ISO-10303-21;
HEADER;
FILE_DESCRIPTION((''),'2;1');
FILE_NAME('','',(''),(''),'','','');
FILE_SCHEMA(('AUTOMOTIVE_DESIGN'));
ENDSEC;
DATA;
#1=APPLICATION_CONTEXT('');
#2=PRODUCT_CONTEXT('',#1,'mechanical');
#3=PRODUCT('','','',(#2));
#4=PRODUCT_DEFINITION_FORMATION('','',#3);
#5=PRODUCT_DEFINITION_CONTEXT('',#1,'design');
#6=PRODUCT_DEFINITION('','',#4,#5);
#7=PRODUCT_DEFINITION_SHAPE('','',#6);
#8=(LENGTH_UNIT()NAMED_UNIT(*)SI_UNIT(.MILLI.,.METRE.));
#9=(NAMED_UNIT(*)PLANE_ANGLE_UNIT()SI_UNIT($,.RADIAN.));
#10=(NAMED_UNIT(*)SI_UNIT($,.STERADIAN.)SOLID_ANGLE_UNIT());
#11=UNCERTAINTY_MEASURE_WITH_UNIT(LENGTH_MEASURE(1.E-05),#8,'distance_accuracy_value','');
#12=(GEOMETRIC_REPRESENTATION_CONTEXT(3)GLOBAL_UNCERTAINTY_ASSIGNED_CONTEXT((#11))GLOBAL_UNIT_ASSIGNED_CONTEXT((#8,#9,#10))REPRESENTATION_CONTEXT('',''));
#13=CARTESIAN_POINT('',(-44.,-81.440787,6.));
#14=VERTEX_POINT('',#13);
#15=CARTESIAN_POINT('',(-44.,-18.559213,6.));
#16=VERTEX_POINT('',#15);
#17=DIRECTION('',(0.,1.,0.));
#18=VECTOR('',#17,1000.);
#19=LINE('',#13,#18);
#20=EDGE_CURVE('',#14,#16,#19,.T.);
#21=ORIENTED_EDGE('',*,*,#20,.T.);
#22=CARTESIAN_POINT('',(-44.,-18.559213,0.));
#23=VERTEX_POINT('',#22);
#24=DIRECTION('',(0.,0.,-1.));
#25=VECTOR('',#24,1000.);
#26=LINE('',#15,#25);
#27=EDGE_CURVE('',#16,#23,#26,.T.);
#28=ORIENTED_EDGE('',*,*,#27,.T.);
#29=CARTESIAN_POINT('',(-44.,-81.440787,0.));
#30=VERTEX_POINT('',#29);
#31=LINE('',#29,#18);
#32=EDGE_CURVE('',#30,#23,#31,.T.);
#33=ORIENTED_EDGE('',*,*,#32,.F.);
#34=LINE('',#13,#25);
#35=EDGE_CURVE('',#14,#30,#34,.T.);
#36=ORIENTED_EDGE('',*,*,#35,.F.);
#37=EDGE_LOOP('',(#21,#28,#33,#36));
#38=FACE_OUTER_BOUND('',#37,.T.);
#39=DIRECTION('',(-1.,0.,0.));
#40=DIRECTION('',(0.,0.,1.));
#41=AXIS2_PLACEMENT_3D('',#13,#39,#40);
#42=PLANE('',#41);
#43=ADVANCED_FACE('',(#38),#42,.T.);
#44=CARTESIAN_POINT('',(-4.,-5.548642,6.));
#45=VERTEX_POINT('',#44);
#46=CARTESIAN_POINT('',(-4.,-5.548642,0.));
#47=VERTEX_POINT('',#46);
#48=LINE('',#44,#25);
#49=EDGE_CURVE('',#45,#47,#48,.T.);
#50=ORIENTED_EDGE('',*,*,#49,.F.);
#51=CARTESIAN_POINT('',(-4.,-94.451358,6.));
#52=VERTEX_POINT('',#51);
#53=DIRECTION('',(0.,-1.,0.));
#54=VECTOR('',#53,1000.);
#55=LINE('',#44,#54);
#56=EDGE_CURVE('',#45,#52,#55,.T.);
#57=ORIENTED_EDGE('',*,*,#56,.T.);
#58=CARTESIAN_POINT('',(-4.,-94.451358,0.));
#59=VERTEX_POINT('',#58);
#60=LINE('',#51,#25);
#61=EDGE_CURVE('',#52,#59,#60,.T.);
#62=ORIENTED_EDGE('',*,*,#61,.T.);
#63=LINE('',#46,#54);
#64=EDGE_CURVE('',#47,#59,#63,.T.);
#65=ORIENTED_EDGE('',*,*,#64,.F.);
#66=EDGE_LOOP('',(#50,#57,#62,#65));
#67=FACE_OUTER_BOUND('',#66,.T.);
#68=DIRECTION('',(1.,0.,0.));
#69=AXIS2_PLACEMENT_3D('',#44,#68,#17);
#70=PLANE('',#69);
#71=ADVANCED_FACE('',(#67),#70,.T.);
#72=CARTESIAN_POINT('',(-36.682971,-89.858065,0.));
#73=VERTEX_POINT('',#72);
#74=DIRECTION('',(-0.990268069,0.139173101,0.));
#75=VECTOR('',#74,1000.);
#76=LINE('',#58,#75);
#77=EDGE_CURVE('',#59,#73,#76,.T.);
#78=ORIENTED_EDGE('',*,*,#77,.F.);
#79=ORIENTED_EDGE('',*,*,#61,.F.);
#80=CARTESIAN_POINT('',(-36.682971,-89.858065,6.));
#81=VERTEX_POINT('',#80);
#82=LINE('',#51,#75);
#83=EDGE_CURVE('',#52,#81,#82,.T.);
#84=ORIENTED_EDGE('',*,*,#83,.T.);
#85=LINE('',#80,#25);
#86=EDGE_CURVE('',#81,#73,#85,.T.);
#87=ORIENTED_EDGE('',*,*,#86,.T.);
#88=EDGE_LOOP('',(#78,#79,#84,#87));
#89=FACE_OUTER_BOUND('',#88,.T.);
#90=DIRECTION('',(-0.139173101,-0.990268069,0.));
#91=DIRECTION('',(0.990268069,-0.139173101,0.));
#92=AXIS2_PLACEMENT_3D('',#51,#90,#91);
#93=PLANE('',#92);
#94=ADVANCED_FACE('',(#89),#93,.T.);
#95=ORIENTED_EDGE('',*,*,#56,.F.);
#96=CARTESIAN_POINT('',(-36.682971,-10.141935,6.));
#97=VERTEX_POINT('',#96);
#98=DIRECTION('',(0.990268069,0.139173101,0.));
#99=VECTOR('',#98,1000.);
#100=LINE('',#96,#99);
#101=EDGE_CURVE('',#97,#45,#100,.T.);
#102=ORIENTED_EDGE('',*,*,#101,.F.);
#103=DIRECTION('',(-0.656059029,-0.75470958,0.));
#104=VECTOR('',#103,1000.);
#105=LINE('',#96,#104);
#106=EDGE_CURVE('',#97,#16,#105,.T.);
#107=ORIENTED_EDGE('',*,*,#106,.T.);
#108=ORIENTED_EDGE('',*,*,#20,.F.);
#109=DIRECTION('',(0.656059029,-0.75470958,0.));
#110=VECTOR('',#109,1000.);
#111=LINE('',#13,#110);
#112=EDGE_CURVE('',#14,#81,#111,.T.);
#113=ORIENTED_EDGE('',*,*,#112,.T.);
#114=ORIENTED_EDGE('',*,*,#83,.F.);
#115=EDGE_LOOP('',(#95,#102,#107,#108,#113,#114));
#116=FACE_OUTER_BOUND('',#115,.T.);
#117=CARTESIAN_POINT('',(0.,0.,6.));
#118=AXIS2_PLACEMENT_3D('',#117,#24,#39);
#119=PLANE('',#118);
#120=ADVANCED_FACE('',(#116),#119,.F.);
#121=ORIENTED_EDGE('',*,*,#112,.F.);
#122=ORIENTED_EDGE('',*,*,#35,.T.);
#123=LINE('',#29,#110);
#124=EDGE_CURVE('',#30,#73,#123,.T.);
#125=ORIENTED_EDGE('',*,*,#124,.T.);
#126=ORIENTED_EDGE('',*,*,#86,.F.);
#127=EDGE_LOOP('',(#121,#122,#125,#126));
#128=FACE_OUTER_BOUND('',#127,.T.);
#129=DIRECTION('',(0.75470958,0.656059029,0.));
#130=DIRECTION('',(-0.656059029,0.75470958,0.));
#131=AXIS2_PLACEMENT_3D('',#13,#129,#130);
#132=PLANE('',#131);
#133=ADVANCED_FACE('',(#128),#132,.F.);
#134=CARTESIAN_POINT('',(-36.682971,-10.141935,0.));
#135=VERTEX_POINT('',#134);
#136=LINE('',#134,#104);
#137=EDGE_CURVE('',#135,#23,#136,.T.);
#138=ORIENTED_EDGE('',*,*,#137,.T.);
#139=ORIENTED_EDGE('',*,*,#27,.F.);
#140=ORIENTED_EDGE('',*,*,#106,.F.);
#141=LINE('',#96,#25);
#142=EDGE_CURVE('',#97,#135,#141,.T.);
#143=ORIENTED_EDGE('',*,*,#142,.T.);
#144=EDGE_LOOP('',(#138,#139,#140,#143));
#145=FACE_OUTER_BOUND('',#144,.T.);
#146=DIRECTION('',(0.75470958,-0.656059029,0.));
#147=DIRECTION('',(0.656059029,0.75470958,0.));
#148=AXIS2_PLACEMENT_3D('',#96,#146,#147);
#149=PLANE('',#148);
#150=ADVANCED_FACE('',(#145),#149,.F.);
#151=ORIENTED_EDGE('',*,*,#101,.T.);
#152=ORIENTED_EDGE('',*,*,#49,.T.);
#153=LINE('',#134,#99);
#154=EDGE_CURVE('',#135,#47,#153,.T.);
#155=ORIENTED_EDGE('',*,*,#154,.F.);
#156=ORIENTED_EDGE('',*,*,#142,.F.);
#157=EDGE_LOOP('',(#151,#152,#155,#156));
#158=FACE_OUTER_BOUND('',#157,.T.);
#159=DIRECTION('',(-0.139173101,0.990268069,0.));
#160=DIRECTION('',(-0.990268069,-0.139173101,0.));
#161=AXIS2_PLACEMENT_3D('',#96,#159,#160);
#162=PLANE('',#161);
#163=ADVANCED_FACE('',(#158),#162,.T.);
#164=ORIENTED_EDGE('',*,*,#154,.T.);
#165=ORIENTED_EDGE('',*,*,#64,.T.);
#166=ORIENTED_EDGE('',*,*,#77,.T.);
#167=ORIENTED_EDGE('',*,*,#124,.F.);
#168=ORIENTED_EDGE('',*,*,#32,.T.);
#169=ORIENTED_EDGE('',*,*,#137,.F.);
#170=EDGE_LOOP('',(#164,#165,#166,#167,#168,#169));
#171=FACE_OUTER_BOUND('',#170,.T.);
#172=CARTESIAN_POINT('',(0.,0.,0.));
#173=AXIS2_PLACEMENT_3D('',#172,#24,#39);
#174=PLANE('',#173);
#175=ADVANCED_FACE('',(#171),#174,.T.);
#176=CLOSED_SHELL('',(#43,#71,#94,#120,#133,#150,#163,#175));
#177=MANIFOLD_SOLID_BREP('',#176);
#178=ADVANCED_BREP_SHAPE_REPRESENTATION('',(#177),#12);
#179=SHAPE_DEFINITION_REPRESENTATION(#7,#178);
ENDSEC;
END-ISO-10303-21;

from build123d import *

# Parameters (mm, degrees)
BOSS_EXTRUDE1_DEPTH = 6


with BuildPart() as part:
    # Sketch1 → Boss-Extrude1 (new body)
    with BuildSketch(Plane.XY):
        Polygon((-4, -94.451357529), (-36.682971358, -89.858065454), (-44, -81.440786869), (-44, -18.559213131), (-36.682971358, -10.141934546), (-4, -5.548642471), align=None)
    extrude(amount=BOSS_EXTRUDE1_DEPTH)


solid = part.part
